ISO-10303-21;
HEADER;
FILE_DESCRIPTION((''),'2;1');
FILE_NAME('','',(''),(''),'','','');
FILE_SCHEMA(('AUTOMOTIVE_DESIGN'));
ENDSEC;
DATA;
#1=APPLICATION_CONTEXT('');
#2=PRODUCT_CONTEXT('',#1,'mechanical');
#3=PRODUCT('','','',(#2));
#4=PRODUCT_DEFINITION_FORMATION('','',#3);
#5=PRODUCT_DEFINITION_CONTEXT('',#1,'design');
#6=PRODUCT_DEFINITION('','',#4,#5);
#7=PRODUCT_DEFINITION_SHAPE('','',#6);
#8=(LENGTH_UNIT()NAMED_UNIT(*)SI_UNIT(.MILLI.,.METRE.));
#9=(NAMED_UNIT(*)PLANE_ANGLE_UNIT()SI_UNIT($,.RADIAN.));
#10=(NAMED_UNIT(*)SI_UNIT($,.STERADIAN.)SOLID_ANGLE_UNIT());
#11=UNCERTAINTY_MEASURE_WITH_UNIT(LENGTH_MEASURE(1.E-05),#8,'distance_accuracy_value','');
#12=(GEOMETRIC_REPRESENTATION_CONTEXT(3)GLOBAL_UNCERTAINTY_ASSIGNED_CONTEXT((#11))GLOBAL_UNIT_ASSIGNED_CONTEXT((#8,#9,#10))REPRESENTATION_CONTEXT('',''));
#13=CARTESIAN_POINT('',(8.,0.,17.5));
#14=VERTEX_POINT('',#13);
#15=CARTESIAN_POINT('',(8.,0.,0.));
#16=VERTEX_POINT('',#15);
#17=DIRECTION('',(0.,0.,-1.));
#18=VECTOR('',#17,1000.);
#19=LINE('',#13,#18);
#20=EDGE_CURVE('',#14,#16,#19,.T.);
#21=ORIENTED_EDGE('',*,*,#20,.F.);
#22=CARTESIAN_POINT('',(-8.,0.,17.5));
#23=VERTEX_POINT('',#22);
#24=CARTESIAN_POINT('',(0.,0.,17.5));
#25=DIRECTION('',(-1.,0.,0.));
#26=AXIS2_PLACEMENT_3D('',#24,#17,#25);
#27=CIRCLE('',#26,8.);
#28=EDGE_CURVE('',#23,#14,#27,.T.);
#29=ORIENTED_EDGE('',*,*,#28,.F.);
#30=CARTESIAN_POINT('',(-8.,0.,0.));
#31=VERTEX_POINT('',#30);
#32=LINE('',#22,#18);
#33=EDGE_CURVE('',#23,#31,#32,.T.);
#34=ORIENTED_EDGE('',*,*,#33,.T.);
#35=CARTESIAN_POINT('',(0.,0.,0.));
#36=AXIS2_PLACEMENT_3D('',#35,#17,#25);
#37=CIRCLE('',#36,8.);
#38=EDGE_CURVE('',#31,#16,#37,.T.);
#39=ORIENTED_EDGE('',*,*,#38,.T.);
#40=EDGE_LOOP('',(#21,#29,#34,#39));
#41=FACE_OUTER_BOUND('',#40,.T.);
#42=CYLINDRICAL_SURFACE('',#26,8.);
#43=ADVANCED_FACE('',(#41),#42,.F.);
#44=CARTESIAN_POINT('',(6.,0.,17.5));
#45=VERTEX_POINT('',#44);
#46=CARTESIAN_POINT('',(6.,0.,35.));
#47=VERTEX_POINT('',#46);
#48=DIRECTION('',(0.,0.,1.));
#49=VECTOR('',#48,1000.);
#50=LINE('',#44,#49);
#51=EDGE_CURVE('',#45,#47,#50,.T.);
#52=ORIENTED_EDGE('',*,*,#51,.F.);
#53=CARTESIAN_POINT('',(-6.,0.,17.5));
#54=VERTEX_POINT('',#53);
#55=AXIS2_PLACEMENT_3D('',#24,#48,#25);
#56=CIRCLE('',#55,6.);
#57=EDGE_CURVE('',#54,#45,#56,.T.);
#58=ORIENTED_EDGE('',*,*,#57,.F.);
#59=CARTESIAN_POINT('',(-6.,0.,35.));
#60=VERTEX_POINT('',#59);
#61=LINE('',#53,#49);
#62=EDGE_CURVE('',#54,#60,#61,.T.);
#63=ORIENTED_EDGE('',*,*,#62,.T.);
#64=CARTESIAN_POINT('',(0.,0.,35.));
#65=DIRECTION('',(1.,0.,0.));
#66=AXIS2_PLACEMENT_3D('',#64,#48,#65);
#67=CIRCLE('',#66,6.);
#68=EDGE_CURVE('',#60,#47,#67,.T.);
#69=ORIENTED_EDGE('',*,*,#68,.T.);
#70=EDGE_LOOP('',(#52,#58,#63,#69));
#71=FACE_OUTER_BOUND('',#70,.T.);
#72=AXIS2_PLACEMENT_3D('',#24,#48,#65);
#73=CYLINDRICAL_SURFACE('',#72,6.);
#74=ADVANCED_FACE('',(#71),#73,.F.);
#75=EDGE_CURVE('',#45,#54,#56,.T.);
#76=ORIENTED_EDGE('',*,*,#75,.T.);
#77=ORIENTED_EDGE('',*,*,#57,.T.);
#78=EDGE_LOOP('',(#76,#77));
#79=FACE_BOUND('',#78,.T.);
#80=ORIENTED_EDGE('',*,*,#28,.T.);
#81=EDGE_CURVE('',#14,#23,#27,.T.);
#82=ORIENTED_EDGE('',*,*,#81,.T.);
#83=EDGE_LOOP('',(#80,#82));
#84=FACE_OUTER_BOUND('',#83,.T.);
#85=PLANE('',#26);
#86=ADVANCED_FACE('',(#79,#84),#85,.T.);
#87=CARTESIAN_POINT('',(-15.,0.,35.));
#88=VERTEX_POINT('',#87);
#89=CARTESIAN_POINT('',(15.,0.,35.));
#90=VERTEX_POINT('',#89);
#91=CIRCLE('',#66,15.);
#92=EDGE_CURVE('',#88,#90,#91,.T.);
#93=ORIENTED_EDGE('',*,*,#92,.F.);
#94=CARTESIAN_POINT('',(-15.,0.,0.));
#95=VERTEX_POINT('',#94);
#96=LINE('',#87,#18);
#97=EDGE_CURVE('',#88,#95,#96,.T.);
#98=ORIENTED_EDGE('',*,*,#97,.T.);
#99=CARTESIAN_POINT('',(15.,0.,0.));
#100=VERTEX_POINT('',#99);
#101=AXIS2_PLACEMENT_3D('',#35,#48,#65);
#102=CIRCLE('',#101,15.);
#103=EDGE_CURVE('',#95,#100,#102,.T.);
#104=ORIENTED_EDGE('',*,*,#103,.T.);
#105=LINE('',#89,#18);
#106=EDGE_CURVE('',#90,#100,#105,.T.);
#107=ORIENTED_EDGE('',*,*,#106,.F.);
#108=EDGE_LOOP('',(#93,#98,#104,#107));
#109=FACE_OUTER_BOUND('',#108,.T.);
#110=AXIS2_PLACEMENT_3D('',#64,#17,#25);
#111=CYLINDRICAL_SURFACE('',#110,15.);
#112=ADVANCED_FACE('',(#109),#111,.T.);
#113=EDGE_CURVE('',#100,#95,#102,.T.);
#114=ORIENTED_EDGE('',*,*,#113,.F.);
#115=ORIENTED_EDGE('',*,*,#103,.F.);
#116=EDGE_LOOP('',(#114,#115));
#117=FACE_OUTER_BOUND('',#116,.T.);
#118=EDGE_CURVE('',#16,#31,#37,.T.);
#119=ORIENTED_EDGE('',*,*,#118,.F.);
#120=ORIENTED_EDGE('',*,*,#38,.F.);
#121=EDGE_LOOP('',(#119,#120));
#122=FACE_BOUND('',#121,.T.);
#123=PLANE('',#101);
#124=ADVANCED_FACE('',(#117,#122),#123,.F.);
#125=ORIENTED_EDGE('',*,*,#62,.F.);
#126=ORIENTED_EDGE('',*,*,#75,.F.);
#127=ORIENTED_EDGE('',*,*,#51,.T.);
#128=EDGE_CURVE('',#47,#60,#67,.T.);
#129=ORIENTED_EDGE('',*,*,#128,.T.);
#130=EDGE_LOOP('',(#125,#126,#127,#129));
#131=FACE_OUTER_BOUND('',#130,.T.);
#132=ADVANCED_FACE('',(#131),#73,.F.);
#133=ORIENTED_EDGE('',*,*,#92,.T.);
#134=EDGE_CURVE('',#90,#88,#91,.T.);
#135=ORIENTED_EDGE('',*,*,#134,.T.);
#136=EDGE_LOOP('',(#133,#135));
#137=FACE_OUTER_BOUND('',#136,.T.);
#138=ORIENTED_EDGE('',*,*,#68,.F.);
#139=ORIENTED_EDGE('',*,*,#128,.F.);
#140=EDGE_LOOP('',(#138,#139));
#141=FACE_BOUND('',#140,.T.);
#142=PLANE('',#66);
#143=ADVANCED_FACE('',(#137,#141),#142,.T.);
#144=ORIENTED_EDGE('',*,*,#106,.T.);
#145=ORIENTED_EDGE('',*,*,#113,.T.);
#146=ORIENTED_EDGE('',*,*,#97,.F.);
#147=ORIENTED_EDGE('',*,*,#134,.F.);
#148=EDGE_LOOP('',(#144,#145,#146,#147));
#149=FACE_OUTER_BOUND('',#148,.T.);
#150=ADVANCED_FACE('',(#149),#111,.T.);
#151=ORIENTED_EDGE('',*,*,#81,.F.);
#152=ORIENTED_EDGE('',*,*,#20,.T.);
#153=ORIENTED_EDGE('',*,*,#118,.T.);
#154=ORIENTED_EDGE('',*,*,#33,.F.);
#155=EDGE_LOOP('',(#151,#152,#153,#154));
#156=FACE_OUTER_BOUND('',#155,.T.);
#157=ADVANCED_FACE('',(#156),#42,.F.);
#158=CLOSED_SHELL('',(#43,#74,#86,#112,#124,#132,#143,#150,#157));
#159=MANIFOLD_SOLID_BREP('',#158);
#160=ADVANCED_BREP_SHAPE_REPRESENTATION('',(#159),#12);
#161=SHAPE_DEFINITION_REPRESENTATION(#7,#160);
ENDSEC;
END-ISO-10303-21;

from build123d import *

# Parameters (mm, degrees)
SKETCH_1_R          = 15
EXTRUDE_1_DEPTH     = 35
SKETCH_2_R          = 6
CUT_EXTRUDE_1_DEPTH = 17.5
SKETCH_3_R          = 8
CUT_EXTRUDE_2_DEPTH = 17.5


with BuildPart() as part:
    # 草图1 → 凸台-拉伸1 (new body)
    with BuildSketch(Plane.XY):
        Circle(SKETCH_1_R)
    extrude(amount=EXTRUDE_1_DEPTH)

    # 草图2 → 切除-拉伸1 (cut)
    with BuildSketch(Plane.XY.offset(35)):
        Circle(SKETCH_2_R)
    extrude(amount=-CUT_EXTRUDE_1_DEPTH, mode=Mode.SUBTRACT)

    # 草图3 → 切除-拉伸2 (cut)
    with BuildSketch(Plane(origin=(0, 0, 0), x_dir=(-1, 0, 0), z_dir=(0, 0, -1))):
        Circle(SKETCH_3_R)
    extrude(amount=-CUT_EXTRUDE_2_DEPTH, mode=Mode.SUBTRACT)


solid = part.part
